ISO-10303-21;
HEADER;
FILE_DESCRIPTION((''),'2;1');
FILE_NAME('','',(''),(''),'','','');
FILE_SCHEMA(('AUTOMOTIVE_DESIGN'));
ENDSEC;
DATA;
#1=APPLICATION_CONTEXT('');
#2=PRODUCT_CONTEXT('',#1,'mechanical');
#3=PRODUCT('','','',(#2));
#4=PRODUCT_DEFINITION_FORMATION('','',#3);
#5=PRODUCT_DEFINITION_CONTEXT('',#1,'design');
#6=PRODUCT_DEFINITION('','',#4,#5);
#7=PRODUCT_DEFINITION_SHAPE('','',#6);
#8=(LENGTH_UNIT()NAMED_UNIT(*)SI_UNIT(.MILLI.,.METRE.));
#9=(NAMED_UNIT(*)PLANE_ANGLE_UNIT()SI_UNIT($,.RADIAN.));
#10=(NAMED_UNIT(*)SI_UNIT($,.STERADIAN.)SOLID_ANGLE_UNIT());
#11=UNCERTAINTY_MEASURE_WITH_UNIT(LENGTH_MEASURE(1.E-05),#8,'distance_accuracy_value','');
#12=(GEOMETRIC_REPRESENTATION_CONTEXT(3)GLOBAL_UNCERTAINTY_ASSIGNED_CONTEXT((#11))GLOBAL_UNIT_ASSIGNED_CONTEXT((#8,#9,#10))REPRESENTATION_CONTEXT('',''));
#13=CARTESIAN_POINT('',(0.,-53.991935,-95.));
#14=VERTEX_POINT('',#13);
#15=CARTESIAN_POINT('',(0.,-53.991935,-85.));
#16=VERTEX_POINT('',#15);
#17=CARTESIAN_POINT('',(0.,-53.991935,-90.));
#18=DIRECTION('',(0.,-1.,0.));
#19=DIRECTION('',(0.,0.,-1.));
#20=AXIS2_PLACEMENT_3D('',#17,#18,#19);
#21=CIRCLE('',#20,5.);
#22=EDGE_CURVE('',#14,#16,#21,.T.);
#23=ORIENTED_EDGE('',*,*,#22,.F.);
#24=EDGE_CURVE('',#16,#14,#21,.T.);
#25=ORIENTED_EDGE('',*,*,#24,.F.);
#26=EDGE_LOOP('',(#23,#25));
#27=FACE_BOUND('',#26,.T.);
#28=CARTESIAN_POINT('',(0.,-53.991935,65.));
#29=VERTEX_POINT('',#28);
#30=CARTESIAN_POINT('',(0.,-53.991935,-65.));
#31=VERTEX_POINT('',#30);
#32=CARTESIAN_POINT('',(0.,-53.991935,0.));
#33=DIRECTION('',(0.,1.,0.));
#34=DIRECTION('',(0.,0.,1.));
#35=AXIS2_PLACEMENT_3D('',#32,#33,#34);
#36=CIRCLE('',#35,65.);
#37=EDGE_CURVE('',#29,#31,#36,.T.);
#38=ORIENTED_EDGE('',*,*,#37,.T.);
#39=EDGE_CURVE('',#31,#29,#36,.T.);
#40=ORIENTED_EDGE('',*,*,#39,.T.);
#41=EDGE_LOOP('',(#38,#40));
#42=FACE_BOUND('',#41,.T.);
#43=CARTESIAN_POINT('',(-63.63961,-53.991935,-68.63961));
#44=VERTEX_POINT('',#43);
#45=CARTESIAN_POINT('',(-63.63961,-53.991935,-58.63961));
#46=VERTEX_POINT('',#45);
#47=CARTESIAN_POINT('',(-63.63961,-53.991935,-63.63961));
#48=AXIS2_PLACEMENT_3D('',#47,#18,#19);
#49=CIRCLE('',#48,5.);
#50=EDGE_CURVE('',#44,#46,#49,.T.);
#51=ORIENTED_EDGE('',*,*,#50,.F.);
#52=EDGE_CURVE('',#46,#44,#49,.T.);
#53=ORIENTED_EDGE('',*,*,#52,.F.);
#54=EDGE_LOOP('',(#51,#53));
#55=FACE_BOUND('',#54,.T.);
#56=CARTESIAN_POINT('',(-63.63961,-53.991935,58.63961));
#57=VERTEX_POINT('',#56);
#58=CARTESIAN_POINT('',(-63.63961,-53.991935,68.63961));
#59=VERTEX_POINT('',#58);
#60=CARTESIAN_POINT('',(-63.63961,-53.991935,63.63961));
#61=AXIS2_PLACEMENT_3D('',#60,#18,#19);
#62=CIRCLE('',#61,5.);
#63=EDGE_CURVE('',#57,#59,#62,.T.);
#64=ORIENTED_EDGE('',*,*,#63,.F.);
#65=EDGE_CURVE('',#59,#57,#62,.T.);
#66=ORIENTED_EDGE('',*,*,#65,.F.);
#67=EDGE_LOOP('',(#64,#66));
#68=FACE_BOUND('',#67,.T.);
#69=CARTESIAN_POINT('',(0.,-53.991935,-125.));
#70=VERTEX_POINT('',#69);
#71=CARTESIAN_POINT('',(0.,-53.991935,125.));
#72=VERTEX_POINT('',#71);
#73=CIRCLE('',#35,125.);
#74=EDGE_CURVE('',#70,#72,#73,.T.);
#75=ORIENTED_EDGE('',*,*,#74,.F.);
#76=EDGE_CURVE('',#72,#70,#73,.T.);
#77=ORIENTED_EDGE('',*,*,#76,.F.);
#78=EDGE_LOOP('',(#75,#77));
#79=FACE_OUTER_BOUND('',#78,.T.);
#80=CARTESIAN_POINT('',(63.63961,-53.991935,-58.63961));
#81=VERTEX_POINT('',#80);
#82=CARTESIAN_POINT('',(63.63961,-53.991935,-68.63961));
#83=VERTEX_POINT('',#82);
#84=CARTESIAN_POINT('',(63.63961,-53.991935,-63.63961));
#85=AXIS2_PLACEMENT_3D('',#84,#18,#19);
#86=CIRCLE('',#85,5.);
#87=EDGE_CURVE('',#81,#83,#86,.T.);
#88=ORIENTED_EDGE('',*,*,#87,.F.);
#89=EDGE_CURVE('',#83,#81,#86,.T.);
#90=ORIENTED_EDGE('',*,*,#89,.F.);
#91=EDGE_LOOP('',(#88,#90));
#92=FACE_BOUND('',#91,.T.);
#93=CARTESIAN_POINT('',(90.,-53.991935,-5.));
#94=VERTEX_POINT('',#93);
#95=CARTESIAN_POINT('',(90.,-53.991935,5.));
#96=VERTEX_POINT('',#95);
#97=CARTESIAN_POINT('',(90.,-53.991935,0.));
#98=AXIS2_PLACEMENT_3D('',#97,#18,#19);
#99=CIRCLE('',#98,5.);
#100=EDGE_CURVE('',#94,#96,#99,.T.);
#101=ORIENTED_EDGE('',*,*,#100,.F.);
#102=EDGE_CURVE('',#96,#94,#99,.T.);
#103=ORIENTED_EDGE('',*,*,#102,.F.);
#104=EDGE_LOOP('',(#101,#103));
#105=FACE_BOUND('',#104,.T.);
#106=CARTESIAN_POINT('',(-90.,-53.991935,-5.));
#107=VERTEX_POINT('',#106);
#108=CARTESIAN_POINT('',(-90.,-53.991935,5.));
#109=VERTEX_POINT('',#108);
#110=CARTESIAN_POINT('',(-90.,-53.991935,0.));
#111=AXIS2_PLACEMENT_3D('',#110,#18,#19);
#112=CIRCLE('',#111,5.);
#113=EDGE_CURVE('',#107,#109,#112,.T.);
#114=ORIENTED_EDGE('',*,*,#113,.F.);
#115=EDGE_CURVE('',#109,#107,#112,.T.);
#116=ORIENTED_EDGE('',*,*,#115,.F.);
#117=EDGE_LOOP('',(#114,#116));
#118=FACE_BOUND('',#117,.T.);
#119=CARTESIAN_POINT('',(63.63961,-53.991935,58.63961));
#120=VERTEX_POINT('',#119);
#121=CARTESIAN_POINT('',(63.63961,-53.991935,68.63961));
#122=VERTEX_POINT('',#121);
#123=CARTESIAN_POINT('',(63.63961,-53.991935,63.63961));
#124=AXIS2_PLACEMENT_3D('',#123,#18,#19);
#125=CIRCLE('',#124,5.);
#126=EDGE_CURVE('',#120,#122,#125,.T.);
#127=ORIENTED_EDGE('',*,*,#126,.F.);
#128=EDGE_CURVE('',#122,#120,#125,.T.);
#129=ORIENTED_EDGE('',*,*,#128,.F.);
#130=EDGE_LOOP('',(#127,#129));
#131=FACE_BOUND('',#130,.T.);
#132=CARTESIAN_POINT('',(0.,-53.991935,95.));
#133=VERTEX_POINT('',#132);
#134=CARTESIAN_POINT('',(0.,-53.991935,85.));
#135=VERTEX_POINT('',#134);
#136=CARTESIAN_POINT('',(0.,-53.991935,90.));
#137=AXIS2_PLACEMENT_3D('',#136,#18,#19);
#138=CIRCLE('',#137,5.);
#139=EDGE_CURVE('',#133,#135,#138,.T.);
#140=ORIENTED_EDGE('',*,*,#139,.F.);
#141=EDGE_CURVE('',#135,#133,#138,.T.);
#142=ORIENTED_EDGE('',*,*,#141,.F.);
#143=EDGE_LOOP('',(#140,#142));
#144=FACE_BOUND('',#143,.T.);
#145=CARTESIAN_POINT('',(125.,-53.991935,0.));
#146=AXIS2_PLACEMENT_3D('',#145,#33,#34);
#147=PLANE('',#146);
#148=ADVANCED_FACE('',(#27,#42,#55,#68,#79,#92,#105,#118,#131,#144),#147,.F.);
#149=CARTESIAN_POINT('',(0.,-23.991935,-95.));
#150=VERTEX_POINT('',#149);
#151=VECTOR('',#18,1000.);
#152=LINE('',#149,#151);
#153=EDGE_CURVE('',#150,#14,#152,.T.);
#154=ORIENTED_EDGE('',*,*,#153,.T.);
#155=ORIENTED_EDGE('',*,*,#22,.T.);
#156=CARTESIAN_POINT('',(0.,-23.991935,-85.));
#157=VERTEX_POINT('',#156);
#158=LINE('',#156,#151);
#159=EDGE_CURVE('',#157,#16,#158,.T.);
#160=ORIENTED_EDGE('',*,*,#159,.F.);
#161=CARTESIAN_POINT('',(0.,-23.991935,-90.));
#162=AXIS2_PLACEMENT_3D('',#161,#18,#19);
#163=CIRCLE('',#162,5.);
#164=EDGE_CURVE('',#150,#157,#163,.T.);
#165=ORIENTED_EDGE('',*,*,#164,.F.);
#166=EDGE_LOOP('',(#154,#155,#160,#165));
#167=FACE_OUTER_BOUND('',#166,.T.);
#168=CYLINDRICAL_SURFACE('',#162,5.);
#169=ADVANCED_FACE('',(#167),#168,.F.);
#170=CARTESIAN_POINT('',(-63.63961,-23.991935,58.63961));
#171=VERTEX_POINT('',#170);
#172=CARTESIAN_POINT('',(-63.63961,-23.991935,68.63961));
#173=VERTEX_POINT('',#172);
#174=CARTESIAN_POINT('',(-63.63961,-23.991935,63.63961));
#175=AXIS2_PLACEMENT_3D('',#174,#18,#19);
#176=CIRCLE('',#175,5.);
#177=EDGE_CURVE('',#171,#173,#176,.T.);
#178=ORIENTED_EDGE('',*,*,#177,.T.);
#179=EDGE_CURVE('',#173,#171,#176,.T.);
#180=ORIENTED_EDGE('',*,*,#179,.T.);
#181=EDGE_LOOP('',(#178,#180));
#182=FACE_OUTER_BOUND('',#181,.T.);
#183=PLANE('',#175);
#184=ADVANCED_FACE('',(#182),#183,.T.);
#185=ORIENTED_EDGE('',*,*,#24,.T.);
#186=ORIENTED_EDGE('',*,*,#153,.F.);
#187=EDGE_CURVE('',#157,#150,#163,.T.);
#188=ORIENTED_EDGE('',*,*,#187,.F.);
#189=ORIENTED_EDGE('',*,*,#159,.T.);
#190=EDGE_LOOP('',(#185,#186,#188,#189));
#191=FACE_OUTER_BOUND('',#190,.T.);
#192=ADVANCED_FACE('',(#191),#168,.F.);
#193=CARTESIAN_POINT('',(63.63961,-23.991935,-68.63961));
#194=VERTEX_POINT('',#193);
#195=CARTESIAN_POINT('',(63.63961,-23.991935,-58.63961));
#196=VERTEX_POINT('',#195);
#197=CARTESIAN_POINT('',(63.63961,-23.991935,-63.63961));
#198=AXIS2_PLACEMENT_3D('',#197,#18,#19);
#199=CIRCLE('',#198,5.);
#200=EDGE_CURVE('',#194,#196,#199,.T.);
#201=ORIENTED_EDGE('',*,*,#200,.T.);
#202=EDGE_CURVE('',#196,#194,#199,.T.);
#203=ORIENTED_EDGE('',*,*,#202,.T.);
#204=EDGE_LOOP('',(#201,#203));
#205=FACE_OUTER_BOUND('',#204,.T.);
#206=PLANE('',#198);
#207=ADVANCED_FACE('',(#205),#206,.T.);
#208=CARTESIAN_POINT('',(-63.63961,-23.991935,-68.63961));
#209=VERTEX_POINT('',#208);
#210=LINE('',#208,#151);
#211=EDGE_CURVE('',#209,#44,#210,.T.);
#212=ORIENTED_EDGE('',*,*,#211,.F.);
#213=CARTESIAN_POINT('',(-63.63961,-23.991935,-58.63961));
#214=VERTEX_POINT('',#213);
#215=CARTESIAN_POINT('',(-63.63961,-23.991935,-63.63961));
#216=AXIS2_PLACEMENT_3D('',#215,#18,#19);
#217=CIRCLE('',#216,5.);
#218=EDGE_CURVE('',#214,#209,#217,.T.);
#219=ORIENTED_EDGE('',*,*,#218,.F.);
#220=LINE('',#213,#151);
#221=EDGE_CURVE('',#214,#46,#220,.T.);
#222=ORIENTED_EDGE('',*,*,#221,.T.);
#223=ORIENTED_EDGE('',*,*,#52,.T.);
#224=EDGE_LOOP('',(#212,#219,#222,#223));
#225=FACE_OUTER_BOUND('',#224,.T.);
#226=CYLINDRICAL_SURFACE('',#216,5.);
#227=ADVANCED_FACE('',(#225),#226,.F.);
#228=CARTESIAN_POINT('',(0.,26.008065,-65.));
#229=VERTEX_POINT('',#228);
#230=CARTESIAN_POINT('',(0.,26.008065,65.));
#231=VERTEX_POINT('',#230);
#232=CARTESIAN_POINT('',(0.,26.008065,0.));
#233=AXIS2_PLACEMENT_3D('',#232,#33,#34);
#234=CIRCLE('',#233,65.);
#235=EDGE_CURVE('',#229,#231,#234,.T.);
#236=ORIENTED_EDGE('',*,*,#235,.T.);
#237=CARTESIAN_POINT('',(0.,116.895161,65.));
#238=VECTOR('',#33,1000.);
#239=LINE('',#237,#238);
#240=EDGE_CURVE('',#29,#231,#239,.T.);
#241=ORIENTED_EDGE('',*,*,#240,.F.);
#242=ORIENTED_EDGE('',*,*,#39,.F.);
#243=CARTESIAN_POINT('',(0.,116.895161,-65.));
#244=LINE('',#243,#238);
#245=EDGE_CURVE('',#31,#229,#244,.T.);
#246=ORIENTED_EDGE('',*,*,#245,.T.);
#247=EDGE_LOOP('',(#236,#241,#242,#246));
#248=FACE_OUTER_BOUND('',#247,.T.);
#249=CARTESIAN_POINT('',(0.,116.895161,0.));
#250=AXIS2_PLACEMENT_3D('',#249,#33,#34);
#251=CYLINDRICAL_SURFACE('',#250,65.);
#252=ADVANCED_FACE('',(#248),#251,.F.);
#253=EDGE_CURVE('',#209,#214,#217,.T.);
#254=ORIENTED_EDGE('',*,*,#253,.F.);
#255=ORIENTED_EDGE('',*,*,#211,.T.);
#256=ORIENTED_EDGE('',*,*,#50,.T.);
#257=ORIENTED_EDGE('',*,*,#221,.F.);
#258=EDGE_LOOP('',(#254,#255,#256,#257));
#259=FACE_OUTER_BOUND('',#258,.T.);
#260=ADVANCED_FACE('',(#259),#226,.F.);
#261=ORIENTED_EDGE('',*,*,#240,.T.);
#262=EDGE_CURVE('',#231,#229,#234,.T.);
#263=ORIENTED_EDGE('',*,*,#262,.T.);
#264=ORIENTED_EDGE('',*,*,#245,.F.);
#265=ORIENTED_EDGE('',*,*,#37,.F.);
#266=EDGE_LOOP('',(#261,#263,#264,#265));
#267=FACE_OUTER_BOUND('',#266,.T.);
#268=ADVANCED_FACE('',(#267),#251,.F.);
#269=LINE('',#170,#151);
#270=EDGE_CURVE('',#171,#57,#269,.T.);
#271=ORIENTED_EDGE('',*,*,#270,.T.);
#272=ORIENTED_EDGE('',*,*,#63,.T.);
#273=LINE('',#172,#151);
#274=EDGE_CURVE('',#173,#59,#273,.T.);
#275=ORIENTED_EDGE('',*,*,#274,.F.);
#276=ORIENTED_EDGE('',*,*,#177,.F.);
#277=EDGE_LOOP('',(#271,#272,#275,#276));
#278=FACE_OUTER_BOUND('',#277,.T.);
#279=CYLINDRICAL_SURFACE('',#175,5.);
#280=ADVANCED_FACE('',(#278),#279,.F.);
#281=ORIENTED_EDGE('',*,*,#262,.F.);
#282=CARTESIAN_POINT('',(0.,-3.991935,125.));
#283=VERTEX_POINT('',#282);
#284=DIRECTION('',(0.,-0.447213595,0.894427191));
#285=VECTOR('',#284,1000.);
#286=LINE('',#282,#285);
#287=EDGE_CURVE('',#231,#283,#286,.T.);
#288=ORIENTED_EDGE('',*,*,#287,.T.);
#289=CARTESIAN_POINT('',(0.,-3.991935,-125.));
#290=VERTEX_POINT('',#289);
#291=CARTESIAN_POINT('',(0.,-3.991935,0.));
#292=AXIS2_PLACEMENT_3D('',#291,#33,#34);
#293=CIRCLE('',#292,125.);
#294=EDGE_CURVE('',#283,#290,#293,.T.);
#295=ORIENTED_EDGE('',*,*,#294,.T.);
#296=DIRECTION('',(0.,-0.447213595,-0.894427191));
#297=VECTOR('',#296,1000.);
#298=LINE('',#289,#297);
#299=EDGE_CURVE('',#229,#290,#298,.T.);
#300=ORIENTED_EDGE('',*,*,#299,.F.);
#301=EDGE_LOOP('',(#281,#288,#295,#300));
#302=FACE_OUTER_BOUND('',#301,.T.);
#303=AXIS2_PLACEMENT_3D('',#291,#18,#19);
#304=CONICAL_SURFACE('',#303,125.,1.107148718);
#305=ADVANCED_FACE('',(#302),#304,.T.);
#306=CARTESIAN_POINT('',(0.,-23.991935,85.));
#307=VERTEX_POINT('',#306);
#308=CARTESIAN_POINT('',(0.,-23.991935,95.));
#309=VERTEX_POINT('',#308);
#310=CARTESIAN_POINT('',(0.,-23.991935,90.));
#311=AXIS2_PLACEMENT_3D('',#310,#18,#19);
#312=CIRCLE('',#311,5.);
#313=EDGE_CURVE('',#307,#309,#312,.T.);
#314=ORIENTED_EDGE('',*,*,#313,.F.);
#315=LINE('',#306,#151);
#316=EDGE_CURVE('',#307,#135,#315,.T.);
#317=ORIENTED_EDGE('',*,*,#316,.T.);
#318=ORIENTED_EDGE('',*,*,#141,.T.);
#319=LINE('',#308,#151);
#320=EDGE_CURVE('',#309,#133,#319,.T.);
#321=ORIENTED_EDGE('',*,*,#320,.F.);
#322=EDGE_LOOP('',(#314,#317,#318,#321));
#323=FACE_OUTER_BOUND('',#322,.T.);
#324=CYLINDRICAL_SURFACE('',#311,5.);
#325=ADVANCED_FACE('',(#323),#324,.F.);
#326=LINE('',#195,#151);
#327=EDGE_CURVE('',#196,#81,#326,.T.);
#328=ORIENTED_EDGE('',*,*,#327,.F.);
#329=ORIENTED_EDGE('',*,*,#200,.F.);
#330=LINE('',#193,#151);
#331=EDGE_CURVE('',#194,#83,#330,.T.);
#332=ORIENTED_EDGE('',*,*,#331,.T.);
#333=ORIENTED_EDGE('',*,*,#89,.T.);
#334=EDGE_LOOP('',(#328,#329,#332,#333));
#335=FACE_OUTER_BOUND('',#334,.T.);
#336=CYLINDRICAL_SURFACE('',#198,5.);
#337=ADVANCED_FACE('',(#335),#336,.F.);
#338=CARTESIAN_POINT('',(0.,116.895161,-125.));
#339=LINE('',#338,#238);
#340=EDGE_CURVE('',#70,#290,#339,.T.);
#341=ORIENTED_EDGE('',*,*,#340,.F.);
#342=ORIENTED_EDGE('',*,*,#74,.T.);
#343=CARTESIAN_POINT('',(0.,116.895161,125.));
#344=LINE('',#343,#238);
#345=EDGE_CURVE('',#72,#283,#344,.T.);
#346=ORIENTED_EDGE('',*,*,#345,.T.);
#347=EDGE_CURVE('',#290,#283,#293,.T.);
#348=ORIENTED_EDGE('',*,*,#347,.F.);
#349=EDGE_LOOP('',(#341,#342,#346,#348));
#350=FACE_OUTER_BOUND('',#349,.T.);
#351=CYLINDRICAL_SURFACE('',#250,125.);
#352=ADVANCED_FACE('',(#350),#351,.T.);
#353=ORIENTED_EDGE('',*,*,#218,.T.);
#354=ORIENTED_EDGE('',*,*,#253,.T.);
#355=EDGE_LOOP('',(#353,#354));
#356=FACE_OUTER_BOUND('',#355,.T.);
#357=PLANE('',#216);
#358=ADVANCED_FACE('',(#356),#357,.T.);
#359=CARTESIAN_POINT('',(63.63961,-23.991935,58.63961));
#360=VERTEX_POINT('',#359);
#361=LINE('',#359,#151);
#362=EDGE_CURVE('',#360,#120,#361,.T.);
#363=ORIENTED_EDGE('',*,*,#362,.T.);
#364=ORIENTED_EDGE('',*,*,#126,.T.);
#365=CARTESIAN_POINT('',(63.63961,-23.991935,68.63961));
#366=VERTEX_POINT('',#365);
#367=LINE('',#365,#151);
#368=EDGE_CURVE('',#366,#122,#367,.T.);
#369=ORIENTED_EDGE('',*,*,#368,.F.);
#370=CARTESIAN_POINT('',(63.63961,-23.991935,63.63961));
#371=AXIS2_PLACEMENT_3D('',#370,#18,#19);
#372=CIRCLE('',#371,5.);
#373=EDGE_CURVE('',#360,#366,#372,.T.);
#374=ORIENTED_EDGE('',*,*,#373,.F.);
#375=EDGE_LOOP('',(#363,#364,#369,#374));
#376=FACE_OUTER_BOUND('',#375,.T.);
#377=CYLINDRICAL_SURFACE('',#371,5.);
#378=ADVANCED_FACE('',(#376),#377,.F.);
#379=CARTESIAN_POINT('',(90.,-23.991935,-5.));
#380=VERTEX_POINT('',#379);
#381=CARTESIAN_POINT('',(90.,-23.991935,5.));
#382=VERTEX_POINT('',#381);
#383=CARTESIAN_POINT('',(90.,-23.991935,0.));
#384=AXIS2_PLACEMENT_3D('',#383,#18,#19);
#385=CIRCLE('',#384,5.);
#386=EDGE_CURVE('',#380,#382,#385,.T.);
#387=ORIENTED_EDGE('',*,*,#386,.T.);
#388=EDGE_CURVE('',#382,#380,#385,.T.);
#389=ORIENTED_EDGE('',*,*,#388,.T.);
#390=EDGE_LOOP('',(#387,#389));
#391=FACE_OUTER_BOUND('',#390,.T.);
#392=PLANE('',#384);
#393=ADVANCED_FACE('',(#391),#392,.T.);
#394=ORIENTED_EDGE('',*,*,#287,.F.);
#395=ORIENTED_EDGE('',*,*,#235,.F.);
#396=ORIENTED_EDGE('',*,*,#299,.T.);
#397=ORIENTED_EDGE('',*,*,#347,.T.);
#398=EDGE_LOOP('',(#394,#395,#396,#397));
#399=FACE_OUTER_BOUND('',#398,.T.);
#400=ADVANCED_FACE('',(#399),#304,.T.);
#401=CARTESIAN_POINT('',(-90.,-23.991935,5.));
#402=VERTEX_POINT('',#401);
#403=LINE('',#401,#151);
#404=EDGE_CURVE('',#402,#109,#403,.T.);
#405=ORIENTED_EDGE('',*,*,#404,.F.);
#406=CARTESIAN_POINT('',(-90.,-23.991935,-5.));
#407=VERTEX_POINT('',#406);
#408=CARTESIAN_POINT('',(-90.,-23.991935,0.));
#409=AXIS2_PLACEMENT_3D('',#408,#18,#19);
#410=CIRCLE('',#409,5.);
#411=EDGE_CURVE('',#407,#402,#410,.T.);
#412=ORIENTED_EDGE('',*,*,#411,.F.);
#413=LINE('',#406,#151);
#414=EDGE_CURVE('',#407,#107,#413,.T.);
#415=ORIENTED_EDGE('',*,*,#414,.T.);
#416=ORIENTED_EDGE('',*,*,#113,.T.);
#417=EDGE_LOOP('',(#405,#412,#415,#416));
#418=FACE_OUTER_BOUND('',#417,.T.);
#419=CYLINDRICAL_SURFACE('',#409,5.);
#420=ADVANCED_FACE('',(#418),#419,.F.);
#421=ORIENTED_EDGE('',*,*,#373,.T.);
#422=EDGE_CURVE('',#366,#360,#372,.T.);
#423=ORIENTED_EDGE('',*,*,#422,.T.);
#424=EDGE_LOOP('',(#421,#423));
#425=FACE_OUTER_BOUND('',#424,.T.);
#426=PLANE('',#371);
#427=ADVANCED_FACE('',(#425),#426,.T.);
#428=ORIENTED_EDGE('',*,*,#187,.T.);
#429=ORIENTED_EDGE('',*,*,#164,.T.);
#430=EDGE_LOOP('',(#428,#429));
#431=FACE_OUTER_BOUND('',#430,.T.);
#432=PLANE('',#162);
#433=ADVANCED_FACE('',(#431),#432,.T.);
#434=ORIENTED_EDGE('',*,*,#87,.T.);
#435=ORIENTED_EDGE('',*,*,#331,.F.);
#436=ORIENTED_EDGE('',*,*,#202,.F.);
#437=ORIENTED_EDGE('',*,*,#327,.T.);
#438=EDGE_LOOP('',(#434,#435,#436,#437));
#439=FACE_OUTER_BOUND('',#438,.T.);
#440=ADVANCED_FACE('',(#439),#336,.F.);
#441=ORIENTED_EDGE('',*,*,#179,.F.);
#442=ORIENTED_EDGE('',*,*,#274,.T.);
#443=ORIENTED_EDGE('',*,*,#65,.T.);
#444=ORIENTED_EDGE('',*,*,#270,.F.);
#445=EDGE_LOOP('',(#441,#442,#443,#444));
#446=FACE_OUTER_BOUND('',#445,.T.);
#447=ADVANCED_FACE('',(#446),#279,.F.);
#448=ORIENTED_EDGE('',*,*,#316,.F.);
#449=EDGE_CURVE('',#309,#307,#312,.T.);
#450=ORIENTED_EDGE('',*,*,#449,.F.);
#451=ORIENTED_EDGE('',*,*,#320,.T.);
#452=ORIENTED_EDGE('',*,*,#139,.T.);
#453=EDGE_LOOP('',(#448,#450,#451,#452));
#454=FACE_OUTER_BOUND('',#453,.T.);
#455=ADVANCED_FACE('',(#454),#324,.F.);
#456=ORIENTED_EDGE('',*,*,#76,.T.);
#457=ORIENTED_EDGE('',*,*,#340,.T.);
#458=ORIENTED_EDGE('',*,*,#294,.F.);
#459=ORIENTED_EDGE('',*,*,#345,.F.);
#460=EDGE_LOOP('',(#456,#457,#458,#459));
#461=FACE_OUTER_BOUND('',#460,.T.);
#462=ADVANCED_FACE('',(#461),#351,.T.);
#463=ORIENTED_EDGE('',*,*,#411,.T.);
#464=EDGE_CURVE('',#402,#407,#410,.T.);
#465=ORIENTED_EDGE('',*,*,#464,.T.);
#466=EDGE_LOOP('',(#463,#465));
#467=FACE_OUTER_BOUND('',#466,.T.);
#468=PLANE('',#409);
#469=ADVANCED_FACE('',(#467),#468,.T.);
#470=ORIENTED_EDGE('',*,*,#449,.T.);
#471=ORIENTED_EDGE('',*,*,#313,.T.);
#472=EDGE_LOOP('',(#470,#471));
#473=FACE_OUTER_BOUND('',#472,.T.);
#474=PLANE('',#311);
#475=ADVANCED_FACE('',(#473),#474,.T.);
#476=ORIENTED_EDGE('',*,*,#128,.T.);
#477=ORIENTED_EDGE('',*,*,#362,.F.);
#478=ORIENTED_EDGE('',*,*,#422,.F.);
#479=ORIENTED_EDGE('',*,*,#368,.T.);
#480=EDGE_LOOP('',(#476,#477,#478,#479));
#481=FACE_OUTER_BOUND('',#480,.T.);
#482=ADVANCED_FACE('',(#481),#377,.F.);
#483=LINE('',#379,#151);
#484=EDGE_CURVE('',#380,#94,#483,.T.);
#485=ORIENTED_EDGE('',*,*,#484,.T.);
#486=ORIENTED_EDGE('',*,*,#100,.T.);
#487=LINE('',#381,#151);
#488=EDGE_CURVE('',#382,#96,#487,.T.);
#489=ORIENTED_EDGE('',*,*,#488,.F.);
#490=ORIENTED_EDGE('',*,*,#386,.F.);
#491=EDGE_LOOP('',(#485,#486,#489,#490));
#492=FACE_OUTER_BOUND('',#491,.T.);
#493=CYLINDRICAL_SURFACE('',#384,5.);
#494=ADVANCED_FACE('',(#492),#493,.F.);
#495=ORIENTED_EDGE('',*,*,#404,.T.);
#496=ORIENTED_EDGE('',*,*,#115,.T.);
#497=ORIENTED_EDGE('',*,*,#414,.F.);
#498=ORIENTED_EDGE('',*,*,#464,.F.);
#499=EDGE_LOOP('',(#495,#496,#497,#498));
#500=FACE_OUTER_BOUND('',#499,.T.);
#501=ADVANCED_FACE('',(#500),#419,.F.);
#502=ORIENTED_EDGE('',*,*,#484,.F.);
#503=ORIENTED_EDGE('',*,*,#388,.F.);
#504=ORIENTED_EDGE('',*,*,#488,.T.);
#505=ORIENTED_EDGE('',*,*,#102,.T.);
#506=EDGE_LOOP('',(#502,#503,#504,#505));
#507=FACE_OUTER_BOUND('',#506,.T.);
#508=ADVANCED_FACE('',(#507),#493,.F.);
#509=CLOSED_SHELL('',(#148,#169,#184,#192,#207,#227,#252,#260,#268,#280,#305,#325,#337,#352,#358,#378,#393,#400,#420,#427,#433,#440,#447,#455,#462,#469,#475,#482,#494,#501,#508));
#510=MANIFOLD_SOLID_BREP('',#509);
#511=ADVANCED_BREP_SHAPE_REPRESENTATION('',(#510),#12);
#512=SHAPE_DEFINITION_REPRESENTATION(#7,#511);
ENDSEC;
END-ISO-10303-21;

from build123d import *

# Parameters (mm, degrees)
SKETCH_2_R          = 5
CUT_EXTRUDE_1_DEPTH = 30


with BuildPart() as part:
    # 草图1 → 旋转1 (revolve)
    with BuildSketch(Plane.XY, mode=Mode.PRIVATE) as revolve_1_sk:
        Polygon((65, -53.991935484), (65, 26.008064516), (125, -3.991935484), (125, -53.991935484), align=None)
    revolve(revolve_1_sk.sketch.rotate(Axis((0, 116.89516129, 0), (0, -1, 0)), 90), axis=Axis((0, 116.89516129, 0), (0, -1, 0)))

    # 草图2 → 切除-拉伸1 (cut)
    with BuildSketch(Plane.XZ.offset(53.991935484)):
        with Locations(Location((90, 0, 0), (0, 0, 270))):
            Circle(SKETCH_2_R)
        with Locations(Location((63.639610307, -63.639610307, 0), (0, 0, 270))):
            Circle(SKETCH_2_R)
        with Locations(Location((0, -90, 0), (0, 0, 270))):
            Circle(SKETCH_2_R)
        with Locations(Location((-63.639610307, -63.639610307, 0), (0, 0, 270))):
            Circle(SKETCH_2_R)
        with Locations(Location((-90, 0, 0), (0, 0, 270))):
            Circle(SKETCH_2_R)
        with Locations(Location((-63.639610307, 63.639610307, 0), (0, 0, 270))):
            Circle(SKETCH_2_R)
        with Locations(Location((0, 90, 0), (0, 0, 270))):
            Circle(SKETCH_2_R)
        with Locations(Location((63.639610307, 63.639610307, 0), (0, 0, 270))):
            Circle(SKETCH_2_R)
    extrude(amount=-CUT_EXTRUDE_1_DEPTH, mode=Mode.SUBTRACT)


solid = part.part
